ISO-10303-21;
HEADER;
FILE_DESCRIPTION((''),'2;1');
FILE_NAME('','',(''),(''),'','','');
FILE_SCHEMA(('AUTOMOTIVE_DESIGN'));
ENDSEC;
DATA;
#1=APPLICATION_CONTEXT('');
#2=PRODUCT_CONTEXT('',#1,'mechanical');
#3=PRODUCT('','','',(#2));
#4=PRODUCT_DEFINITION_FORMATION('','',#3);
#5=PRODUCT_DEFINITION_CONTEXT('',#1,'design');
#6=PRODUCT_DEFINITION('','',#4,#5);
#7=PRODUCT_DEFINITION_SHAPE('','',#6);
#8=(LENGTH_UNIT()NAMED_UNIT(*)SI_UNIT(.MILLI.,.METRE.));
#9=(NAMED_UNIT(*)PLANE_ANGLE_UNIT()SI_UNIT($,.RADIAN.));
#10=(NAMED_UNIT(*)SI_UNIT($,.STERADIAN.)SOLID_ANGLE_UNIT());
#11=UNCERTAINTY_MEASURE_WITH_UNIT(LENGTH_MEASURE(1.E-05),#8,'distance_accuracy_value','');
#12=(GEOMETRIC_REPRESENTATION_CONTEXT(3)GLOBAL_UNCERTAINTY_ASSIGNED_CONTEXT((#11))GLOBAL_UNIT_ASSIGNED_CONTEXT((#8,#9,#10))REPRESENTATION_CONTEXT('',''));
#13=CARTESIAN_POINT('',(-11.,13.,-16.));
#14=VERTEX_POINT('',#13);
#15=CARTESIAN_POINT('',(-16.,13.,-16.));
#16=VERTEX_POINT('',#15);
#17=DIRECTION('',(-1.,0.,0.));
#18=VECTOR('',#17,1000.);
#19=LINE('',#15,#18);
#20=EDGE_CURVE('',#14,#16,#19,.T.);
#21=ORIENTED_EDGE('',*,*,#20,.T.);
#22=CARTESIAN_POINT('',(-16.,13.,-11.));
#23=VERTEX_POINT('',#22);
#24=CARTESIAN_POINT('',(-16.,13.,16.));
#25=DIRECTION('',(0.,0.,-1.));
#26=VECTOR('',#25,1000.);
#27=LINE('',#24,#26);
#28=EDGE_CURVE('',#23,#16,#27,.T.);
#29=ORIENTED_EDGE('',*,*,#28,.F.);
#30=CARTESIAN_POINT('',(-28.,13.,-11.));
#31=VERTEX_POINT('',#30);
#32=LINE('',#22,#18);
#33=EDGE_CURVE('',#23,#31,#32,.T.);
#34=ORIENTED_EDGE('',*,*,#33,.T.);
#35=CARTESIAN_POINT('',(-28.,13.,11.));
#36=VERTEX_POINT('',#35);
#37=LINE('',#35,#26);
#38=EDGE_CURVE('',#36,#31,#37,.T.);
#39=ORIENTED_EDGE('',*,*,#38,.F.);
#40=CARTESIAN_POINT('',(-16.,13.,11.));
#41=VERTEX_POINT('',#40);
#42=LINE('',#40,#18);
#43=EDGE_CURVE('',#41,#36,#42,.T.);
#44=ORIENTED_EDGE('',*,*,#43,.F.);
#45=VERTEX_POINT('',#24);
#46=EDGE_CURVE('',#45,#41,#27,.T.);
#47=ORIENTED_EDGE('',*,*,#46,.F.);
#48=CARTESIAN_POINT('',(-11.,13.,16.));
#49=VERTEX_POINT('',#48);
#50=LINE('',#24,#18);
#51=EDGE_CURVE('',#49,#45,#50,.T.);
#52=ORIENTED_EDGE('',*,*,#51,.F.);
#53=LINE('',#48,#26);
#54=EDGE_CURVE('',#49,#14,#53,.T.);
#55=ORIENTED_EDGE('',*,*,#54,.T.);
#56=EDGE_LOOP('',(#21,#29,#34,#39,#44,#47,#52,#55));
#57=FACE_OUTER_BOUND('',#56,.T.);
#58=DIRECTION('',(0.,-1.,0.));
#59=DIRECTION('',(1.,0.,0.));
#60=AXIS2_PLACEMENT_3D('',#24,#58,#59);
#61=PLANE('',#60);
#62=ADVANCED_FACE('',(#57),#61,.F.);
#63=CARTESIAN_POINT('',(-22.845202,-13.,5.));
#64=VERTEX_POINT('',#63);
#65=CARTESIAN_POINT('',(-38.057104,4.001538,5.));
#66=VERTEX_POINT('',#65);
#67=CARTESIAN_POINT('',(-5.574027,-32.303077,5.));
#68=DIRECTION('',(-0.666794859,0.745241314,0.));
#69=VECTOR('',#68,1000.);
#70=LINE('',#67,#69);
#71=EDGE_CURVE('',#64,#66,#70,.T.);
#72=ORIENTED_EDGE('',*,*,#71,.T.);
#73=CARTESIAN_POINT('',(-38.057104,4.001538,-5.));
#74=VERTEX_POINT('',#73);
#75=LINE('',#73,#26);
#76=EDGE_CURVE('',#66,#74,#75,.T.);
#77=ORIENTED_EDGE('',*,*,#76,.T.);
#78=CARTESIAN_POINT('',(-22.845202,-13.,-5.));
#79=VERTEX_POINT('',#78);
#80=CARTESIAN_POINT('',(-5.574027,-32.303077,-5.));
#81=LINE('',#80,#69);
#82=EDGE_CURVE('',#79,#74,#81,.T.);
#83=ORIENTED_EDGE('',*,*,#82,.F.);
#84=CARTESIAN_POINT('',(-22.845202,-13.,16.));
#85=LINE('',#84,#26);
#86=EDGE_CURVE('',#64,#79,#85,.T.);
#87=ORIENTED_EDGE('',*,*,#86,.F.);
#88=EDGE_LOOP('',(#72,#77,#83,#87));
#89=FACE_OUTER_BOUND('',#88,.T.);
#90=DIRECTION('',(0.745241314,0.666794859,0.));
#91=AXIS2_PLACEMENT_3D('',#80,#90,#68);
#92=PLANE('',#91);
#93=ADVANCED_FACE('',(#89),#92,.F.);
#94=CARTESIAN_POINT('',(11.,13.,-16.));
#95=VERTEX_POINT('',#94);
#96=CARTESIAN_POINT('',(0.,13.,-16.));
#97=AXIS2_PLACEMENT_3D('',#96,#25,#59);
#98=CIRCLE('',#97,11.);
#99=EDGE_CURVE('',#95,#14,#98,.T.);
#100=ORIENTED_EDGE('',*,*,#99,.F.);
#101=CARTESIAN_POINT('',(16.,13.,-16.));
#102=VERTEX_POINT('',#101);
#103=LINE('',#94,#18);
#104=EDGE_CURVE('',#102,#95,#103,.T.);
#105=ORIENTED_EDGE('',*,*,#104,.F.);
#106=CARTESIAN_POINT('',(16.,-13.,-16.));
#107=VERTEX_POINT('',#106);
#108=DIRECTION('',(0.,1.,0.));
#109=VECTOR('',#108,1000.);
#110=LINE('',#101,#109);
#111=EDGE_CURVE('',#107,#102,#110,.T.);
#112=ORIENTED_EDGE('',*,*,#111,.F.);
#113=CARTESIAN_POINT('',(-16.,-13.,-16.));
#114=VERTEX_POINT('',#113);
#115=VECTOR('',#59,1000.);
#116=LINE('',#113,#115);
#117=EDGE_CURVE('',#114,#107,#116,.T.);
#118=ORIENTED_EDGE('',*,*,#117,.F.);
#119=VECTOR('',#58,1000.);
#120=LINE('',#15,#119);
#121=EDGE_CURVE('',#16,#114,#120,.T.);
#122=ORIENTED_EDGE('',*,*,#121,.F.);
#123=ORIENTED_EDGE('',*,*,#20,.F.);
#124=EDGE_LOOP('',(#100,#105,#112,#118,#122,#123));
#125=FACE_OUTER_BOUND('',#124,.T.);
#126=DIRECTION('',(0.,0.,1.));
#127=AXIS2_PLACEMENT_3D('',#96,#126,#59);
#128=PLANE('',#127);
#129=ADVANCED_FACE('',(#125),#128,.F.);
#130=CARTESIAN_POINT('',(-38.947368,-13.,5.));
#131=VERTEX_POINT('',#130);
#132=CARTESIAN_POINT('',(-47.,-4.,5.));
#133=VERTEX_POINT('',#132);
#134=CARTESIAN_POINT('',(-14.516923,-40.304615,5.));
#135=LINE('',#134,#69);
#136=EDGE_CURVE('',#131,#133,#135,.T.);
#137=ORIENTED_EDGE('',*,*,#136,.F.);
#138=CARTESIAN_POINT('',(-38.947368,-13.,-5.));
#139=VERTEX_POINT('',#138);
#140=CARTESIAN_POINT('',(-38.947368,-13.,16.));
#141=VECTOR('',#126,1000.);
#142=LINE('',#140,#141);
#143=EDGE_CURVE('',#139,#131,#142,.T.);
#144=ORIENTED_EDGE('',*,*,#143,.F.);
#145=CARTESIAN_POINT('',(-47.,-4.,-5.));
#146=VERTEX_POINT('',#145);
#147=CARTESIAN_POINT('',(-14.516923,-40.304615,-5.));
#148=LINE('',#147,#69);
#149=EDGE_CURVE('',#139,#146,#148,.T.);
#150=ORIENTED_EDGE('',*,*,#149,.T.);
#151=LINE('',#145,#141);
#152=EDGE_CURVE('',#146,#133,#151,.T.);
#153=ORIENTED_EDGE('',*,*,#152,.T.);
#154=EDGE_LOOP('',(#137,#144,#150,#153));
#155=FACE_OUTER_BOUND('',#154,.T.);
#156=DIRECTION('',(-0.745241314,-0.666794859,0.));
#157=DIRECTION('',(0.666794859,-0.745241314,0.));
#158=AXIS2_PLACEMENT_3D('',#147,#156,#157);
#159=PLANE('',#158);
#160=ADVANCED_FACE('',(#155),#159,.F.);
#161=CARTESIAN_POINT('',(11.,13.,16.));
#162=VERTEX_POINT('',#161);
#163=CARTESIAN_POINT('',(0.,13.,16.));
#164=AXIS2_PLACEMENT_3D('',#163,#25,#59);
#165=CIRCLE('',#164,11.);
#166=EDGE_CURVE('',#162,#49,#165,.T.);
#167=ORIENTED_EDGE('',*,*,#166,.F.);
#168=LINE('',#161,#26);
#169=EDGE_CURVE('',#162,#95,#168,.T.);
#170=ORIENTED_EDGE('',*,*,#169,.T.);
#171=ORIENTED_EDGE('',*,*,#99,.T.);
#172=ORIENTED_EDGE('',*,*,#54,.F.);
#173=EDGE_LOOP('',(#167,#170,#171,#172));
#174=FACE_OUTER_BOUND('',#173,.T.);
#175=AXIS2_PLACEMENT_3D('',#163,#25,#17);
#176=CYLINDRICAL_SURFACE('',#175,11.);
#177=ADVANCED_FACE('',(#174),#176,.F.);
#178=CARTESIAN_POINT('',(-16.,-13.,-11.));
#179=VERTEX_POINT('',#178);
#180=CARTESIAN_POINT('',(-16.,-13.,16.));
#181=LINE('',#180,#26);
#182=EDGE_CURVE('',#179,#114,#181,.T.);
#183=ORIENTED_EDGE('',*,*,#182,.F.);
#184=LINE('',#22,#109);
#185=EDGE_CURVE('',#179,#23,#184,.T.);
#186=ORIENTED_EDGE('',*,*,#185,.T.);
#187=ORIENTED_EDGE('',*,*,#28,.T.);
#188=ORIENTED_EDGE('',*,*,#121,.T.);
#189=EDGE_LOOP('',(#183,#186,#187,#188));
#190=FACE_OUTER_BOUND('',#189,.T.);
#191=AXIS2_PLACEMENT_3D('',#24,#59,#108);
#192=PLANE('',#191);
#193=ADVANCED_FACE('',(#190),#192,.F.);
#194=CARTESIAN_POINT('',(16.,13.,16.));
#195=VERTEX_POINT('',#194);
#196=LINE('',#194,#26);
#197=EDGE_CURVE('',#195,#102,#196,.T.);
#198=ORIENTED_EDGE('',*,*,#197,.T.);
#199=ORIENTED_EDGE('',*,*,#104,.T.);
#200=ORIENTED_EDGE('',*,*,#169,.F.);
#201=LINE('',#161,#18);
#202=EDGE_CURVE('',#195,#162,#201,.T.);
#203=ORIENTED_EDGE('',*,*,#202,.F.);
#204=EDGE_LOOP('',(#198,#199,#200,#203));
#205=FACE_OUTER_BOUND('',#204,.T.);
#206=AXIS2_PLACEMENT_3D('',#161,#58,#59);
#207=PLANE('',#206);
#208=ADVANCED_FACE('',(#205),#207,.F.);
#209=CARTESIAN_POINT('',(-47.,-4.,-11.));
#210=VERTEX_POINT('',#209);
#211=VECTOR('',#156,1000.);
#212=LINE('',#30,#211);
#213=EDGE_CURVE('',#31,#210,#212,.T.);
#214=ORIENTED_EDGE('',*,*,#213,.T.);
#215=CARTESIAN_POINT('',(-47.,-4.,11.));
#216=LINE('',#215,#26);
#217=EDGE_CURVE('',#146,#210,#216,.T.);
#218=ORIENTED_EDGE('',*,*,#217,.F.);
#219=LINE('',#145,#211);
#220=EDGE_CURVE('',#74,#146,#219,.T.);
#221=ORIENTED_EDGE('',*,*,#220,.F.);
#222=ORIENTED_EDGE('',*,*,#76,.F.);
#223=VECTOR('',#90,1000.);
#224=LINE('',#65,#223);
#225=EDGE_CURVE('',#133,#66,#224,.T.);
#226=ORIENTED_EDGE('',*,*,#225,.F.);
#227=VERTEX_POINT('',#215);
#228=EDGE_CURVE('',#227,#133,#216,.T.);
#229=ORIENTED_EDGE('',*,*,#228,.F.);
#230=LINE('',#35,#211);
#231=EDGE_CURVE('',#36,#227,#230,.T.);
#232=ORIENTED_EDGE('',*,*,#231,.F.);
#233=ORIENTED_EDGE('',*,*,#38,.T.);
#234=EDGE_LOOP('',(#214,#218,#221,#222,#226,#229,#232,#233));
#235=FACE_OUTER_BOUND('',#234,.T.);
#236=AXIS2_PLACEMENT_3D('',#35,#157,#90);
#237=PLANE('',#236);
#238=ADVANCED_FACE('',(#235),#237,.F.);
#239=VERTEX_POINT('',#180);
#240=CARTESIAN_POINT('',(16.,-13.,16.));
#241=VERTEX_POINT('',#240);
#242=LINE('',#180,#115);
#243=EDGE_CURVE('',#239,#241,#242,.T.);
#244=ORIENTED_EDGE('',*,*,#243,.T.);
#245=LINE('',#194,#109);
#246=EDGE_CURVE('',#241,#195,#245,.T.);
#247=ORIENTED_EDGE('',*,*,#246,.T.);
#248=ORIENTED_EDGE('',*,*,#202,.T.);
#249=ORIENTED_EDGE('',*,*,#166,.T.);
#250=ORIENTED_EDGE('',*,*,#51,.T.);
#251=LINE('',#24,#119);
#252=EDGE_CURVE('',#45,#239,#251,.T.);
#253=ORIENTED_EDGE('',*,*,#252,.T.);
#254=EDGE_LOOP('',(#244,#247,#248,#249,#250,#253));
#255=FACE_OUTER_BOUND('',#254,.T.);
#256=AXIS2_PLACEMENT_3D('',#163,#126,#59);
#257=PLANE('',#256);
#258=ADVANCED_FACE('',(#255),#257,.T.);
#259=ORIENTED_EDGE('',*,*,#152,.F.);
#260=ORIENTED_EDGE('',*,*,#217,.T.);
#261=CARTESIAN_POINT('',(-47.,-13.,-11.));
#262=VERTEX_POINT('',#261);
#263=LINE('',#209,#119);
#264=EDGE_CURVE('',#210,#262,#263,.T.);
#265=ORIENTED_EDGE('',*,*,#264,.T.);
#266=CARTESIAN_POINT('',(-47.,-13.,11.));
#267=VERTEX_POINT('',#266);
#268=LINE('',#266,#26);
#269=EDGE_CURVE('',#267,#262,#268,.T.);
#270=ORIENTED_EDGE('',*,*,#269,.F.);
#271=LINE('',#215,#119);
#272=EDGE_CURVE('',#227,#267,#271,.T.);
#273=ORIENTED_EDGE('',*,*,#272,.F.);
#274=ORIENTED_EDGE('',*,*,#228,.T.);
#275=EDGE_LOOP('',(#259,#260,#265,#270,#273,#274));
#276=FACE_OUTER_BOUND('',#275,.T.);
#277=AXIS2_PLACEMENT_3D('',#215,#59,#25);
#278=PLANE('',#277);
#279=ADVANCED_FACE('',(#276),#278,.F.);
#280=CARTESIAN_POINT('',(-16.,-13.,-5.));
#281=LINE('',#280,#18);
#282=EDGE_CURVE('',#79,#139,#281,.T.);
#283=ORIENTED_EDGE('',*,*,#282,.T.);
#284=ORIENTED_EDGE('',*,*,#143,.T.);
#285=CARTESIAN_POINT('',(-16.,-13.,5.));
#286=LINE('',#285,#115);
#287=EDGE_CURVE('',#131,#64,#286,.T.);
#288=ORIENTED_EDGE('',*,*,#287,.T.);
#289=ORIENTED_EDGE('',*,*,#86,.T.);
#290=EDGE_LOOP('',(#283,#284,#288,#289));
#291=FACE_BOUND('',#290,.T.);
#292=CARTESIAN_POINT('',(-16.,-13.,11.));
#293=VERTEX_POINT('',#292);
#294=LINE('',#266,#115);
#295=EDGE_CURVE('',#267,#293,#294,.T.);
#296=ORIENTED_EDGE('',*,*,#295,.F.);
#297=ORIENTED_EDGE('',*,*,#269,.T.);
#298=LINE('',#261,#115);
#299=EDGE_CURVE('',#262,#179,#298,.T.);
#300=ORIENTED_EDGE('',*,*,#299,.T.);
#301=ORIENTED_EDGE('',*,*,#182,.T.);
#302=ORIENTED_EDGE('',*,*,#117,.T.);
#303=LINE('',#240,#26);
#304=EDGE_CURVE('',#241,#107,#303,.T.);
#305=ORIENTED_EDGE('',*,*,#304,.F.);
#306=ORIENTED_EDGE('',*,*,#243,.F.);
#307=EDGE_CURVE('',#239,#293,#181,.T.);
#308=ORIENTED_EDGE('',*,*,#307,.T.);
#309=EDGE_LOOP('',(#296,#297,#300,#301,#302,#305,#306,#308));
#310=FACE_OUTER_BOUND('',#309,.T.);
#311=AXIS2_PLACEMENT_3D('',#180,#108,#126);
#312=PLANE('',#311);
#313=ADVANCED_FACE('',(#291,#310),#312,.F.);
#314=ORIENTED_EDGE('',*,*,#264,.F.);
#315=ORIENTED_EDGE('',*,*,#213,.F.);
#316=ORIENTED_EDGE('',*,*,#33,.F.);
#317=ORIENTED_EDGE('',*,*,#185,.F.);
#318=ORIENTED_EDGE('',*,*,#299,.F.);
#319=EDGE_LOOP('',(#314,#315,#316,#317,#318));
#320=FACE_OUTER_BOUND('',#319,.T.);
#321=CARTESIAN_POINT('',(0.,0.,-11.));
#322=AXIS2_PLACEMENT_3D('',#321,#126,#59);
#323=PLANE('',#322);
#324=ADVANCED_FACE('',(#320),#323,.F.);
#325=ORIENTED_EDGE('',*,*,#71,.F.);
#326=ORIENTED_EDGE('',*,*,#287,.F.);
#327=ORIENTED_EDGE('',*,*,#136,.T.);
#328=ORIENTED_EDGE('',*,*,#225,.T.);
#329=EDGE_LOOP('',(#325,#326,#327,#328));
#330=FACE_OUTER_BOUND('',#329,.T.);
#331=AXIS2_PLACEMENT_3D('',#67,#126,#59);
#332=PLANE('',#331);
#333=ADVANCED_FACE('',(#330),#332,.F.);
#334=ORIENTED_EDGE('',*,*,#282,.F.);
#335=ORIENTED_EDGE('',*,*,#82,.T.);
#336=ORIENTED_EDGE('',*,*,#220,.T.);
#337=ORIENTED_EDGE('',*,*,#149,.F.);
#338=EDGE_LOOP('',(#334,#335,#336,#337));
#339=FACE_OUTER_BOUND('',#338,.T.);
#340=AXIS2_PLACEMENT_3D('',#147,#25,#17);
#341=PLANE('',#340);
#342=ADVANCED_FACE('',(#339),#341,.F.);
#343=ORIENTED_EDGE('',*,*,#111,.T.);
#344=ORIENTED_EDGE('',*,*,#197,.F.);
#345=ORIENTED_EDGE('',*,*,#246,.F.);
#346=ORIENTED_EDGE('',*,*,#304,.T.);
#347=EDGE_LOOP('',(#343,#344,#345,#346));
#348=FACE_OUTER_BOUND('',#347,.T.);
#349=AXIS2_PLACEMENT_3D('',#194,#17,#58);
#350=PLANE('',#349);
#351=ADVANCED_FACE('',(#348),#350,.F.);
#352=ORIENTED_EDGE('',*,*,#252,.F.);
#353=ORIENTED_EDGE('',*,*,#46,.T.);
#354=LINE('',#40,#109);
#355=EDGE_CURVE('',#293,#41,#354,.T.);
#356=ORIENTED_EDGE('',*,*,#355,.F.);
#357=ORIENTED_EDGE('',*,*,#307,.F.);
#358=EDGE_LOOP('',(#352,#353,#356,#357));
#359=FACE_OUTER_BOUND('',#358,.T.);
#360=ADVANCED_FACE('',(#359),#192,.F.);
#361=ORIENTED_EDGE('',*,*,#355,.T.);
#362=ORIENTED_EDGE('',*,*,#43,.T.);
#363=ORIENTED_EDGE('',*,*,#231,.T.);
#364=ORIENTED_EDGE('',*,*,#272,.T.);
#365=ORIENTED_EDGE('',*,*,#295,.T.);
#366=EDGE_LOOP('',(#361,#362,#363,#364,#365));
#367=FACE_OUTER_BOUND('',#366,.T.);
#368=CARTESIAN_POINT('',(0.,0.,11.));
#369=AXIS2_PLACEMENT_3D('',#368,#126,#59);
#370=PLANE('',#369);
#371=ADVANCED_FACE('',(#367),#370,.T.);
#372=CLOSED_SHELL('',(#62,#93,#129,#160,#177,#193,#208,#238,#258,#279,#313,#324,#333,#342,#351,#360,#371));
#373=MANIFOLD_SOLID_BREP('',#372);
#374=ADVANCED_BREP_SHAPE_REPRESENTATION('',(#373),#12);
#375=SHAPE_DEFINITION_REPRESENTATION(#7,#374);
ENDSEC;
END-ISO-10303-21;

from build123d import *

# Parameters (mm, degrees)
CRADLE_BLOCK_DEPTH      = 16
TAPERED_EXTENSION_DEPTH = 11
RELIEF_SLOT_PROFILE_W   = 12
RELIEF_SLOT_PROFILE_H   = 10
RELIEF_SLOT_DEPTH       = 52.378729511


with BuildPart() as part:
    # Cradle Block Profile → Cradle Block (new, symmetric)
    with BuildSketch(Plane.XY):
        with BuildLine():
            Line((11, 13), (16, 13))
            Line((16, 13), (16, -13))
            Line((16, -13), (-16, -13))
            Line((-16, -13), (-16, 13))
            Line((-16, 13), (-11, 13))
            ThreePointArc((-11, 13), (0, 2), (11, 13))
        make_face()
    extrude(amount=CRADLE_BLOCK_DEPTH, both=True)

    # Tapered Extension Profile → Tapered Extension (add, symmetric)
    with BuildSketch(Plane.XY):
        Polygon((-16, 13), (-28, 13), (-47, -4), (-47, -13), (-16, -13), align=None)
    extrude(amount=TAPERED_EXTENSION_DEPTH, both=True)

    # Relief Slot Profile → Relief Slot (cut, through all)
    with BuildSketch(Plane(origin=(-18.909230769, 21.133846154, 0), x_dir=(0.745241313525099, 0.6667948594698261, 0), z_dir=(-0.6667948594698261, 0.745241313525099, 0))):
        with Locations((-31.693521174, 0)):
            Rectangle(RELIEF_SLOT_PROFILE_W, RELIEF_SLOT_PROFILE_H)
    extrude(amount=-RELIEF_SLOT_DEPTH, mode=Mode.SUBTRACT)


solid = part.part
